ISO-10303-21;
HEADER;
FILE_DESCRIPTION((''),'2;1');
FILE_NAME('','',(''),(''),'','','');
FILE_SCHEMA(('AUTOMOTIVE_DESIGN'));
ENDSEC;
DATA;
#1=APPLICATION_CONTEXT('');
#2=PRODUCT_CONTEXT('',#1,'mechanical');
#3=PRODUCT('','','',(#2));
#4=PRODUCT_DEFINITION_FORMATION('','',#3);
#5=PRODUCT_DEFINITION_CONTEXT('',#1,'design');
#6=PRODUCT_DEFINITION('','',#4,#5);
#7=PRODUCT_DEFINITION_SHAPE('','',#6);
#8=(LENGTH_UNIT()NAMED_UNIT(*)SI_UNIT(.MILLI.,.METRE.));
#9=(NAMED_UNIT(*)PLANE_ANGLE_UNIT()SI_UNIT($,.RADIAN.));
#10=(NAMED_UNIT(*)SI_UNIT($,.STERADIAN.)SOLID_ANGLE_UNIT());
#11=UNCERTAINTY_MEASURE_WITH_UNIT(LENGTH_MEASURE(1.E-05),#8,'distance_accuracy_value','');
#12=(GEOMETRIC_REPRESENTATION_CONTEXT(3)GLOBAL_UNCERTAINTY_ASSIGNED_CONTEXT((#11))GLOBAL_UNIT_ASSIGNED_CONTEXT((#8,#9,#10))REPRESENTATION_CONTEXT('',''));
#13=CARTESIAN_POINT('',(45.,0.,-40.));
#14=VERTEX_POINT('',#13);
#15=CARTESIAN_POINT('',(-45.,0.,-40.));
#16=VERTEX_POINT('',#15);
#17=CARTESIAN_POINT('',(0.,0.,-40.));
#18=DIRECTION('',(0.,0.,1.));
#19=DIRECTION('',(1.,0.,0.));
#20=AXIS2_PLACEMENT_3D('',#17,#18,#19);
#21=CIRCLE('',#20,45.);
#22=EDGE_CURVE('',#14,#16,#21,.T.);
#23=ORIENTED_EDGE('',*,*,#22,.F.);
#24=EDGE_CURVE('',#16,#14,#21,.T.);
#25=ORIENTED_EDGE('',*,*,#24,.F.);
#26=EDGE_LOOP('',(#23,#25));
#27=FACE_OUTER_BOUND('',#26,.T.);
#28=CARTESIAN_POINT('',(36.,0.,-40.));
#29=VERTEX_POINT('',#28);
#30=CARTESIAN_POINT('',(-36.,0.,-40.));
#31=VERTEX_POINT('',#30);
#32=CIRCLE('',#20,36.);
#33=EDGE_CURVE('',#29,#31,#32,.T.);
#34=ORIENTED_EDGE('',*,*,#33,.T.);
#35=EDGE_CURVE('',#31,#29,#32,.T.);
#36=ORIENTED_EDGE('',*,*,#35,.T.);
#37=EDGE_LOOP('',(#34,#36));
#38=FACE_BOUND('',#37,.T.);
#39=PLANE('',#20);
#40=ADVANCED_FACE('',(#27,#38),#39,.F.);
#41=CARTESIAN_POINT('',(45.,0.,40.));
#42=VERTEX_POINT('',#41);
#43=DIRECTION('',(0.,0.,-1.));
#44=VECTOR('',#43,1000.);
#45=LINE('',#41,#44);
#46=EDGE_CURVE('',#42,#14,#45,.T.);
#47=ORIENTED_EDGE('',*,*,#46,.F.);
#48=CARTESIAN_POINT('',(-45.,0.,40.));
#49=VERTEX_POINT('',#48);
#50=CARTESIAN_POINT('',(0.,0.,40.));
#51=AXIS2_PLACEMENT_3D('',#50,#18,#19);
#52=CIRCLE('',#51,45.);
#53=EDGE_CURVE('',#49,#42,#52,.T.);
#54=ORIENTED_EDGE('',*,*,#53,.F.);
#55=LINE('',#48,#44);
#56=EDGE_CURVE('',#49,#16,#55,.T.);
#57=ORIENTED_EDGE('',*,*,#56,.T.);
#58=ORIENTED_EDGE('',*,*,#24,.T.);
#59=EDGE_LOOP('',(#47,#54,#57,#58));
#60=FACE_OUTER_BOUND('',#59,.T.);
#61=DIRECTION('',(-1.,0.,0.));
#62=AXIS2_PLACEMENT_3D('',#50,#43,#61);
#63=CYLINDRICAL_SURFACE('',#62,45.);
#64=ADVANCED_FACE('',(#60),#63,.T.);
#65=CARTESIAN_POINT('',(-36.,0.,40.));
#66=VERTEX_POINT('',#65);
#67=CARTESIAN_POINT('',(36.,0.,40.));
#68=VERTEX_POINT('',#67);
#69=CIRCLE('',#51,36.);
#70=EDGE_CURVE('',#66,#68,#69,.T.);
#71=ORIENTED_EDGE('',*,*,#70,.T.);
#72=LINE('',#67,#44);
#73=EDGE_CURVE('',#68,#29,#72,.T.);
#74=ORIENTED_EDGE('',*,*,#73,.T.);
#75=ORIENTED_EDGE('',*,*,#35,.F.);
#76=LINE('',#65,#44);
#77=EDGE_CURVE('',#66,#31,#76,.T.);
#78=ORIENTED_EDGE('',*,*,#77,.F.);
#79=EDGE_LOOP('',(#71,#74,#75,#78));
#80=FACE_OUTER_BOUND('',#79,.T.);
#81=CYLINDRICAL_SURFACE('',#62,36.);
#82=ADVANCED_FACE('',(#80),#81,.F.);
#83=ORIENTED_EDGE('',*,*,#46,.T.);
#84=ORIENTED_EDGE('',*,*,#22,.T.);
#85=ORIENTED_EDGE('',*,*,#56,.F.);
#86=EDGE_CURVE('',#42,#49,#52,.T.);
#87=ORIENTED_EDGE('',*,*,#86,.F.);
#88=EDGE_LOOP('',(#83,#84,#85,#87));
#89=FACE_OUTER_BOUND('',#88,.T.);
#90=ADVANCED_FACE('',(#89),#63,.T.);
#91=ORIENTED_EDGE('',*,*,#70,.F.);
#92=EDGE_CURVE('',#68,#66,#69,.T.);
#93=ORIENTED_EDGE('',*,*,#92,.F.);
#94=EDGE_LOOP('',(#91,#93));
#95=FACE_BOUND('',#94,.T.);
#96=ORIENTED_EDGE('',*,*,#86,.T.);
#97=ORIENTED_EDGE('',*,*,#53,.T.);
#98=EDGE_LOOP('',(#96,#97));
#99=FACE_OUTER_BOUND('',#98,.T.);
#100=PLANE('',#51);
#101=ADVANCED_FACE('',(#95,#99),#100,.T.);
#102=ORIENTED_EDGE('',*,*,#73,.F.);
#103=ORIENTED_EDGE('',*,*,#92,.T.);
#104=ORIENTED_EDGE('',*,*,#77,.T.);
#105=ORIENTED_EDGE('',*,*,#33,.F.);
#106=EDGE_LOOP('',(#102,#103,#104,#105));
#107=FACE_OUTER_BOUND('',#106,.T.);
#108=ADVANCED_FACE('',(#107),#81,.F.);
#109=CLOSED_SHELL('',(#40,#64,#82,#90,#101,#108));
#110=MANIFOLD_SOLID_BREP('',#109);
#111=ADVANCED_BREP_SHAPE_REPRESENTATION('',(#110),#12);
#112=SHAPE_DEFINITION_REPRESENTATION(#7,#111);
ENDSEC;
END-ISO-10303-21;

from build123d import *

# Parameters (mm, degrees)
SKETCH_1_R      = 45
SKETCH_1_R_2    = 36
EXTRUDE_1_DEPTH = 40


with BuildPart() as part:
    # 草图1 → 凸台-拉伸1 (new, symmetric)
    with BuildSketch(Plane.XY):
        Circle(SKETCH_1_R)
        Circle(SKETCH_1_R_2, mode=Mode.SUBTRACT)
    extrude(amount=EXTRUDE_1_DEPTH, both=True)


solid = part.part
